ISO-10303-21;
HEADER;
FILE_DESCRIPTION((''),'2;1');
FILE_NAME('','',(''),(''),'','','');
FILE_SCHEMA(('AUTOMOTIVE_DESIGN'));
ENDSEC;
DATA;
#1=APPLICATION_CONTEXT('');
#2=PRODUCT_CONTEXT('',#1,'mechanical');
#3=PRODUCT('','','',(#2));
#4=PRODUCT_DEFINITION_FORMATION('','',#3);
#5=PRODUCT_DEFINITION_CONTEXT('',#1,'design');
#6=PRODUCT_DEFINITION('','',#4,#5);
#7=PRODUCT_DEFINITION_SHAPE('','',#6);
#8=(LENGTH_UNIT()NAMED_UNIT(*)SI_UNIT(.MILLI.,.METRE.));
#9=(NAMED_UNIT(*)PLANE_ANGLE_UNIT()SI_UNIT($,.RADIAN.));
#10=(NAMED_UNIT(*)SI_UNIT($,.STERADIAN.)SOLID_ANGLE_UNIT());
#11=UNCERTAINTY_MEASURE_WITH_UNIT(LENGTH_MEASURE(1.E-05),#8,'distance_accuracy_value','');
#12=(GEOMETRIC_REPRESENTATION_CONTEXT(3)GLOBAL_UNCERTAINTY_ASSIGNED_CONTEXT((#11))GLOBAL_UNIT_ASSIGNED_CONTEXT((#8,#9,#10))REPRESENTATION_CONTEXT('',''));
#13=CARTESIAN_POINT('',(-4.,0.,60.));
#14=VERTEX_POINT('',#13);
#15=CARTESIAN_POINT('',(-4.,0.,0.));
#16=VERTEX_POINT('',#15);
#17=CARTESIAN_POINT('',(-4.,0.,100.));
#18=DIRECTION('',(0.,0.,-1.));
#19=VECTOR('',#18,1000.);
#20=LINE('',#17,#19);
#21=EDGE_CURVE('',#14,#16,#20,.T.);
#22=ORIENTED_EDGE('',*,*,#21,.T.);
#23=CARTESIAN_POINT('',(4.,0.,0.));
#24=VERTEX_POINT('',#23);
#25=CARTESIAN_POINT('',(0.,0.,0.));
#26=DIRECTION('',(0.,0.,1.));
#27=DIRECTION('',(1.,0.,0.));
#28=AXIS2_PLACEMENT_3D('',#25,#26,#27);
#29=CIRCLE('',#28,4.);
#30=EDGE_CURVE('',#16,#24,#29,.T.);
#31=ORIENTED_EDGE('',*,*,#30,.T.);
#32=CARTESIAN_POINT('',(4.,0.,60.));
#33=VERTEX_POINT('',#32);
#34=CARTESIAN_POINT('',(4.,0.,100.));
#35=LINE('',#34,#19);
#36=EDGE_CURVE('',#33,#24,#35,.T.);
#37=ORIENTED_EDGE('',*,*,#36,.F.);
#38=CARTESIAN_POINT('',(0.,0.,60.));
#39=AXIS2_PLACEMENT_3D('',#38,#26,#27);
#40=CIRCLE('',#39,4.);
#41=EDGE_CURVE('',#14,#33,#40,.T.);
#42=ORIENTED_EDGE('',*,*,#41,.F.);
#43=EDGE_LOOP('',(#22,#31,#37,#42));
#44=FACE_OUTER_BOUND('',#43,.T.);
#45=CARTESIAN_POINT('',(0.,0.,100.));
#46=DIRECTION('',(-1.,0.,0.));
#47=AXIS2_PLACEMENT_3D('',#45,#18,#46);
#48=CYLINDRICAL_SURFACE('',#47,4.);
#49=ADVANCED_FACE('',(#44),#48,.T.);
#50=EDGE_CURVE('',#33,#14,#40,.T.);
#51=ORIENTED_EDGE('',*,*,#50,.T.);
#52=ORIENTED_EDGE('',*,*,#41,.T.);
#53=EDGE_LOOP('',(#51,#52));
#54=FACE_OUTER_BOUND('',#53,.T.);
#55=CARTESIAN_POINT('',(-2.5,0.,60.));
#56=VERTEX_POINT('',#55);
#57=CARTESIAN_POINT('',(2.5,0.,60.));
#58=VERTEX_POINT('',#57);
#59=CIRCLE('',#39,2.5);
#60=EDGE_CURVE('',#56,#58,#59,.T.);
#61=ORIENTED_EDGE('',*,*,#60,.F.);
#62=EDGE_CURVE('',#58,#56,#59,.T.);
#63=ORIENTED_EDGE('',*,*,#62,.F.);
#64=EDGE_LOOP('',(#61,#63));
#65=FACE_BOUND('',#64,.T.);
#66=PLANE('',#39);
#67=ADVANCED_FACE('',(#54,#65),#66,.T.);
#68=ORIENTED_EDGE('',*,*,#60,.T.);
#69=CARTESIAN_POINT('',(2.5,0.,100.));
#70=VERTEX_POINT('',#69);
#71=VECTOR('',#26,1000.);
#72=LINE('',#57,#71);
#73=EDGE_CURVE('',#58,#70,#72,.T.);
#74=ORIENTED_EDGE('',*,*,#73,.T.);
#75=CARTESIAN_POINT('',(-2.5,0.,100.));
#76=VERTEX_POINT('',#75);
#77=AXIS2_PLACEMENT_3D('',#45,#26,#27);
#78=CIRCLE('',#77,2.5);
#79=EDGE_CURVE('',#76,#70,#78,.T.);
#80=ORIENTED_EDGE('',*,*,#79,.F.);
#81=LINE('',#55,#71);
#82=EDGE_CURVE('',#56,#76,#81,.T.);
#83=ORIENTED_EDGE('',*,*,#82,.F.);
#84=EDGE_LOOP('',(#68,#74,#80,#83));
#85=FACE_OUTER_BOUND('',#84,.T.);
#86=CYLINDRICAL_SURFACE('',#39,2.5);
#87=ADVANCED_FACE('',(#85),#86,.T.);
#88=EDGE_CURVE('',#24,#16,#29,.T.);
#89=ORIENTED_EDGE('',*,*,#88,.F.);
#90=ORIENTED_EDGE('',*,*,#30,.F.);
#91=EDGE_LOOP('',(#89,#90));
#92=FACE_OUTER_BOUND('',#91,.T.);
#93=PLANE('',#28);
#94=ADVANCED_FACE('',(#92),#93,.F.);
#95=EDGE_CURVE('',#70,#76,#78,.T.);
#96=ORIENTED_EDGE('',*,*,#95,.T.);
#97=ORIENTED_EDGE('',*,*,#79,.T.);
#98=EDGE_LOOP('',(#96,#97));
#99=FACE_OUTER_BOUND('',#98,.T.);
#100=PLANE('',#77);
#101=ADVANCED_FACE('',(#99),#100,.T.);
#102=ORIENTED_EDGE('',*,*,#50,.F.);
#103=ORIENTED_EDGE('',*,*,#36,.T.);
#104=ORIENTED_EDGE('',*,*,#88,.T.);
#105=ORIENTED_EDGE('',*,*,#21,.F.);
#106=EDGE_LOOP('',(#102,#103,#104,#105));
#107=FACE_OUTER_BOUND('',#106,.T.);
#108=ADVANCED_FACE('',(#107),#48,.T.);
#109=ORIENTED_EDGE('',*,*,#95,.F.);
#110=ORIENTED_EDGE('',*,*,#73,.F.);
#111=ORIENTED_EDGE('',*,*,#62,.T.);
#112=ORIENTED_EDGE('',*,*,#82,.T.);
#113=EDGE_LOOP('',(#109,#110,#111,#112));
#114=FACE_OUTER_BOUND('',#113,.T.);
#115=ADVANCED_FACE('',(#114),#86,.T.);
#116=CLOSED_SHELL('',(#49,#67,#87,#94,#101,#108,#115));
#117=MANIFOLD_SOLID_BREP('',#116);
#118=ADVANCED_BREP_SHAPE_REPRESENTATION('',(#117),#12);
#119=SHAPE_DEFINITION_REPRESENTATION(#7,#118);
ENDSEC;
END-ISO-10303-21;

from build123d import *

# Parameters (mm, degrees)
SKETCH_1_R          = 4
EXTRUDE_1_DEPTH     = 100
CUT_EXTRUDE_START   = -40
SKETCH_2_R          = 4
SKETCH_2_R_2        = 2.5
CUT_EXTRUDE_1_DEPTH = 40


with BuildPart() as part:
    # 草图1 → 凸台-拉伸1 (new body)
    with BuildSketch(Plane.XY):
        Circle(SKETCH_1_R)
    extrude(amount=EXTRUDE_1_DEPTH)

    # 草图2 → 切除-拉伸1 (cut)
    with BuildSketch(Plane.XY.offset(100).offset(CUT_EXTRUDE_START)):
        Circle(SKETCH_2_R)
        Circle(SKETCH_2_R_2, mode=Mode.SUBTRACT)
    extrude(amount=CUT_EXTRUDE_1_DEPTH, mode=Mode.SUBTRACT)


solid = part.part
